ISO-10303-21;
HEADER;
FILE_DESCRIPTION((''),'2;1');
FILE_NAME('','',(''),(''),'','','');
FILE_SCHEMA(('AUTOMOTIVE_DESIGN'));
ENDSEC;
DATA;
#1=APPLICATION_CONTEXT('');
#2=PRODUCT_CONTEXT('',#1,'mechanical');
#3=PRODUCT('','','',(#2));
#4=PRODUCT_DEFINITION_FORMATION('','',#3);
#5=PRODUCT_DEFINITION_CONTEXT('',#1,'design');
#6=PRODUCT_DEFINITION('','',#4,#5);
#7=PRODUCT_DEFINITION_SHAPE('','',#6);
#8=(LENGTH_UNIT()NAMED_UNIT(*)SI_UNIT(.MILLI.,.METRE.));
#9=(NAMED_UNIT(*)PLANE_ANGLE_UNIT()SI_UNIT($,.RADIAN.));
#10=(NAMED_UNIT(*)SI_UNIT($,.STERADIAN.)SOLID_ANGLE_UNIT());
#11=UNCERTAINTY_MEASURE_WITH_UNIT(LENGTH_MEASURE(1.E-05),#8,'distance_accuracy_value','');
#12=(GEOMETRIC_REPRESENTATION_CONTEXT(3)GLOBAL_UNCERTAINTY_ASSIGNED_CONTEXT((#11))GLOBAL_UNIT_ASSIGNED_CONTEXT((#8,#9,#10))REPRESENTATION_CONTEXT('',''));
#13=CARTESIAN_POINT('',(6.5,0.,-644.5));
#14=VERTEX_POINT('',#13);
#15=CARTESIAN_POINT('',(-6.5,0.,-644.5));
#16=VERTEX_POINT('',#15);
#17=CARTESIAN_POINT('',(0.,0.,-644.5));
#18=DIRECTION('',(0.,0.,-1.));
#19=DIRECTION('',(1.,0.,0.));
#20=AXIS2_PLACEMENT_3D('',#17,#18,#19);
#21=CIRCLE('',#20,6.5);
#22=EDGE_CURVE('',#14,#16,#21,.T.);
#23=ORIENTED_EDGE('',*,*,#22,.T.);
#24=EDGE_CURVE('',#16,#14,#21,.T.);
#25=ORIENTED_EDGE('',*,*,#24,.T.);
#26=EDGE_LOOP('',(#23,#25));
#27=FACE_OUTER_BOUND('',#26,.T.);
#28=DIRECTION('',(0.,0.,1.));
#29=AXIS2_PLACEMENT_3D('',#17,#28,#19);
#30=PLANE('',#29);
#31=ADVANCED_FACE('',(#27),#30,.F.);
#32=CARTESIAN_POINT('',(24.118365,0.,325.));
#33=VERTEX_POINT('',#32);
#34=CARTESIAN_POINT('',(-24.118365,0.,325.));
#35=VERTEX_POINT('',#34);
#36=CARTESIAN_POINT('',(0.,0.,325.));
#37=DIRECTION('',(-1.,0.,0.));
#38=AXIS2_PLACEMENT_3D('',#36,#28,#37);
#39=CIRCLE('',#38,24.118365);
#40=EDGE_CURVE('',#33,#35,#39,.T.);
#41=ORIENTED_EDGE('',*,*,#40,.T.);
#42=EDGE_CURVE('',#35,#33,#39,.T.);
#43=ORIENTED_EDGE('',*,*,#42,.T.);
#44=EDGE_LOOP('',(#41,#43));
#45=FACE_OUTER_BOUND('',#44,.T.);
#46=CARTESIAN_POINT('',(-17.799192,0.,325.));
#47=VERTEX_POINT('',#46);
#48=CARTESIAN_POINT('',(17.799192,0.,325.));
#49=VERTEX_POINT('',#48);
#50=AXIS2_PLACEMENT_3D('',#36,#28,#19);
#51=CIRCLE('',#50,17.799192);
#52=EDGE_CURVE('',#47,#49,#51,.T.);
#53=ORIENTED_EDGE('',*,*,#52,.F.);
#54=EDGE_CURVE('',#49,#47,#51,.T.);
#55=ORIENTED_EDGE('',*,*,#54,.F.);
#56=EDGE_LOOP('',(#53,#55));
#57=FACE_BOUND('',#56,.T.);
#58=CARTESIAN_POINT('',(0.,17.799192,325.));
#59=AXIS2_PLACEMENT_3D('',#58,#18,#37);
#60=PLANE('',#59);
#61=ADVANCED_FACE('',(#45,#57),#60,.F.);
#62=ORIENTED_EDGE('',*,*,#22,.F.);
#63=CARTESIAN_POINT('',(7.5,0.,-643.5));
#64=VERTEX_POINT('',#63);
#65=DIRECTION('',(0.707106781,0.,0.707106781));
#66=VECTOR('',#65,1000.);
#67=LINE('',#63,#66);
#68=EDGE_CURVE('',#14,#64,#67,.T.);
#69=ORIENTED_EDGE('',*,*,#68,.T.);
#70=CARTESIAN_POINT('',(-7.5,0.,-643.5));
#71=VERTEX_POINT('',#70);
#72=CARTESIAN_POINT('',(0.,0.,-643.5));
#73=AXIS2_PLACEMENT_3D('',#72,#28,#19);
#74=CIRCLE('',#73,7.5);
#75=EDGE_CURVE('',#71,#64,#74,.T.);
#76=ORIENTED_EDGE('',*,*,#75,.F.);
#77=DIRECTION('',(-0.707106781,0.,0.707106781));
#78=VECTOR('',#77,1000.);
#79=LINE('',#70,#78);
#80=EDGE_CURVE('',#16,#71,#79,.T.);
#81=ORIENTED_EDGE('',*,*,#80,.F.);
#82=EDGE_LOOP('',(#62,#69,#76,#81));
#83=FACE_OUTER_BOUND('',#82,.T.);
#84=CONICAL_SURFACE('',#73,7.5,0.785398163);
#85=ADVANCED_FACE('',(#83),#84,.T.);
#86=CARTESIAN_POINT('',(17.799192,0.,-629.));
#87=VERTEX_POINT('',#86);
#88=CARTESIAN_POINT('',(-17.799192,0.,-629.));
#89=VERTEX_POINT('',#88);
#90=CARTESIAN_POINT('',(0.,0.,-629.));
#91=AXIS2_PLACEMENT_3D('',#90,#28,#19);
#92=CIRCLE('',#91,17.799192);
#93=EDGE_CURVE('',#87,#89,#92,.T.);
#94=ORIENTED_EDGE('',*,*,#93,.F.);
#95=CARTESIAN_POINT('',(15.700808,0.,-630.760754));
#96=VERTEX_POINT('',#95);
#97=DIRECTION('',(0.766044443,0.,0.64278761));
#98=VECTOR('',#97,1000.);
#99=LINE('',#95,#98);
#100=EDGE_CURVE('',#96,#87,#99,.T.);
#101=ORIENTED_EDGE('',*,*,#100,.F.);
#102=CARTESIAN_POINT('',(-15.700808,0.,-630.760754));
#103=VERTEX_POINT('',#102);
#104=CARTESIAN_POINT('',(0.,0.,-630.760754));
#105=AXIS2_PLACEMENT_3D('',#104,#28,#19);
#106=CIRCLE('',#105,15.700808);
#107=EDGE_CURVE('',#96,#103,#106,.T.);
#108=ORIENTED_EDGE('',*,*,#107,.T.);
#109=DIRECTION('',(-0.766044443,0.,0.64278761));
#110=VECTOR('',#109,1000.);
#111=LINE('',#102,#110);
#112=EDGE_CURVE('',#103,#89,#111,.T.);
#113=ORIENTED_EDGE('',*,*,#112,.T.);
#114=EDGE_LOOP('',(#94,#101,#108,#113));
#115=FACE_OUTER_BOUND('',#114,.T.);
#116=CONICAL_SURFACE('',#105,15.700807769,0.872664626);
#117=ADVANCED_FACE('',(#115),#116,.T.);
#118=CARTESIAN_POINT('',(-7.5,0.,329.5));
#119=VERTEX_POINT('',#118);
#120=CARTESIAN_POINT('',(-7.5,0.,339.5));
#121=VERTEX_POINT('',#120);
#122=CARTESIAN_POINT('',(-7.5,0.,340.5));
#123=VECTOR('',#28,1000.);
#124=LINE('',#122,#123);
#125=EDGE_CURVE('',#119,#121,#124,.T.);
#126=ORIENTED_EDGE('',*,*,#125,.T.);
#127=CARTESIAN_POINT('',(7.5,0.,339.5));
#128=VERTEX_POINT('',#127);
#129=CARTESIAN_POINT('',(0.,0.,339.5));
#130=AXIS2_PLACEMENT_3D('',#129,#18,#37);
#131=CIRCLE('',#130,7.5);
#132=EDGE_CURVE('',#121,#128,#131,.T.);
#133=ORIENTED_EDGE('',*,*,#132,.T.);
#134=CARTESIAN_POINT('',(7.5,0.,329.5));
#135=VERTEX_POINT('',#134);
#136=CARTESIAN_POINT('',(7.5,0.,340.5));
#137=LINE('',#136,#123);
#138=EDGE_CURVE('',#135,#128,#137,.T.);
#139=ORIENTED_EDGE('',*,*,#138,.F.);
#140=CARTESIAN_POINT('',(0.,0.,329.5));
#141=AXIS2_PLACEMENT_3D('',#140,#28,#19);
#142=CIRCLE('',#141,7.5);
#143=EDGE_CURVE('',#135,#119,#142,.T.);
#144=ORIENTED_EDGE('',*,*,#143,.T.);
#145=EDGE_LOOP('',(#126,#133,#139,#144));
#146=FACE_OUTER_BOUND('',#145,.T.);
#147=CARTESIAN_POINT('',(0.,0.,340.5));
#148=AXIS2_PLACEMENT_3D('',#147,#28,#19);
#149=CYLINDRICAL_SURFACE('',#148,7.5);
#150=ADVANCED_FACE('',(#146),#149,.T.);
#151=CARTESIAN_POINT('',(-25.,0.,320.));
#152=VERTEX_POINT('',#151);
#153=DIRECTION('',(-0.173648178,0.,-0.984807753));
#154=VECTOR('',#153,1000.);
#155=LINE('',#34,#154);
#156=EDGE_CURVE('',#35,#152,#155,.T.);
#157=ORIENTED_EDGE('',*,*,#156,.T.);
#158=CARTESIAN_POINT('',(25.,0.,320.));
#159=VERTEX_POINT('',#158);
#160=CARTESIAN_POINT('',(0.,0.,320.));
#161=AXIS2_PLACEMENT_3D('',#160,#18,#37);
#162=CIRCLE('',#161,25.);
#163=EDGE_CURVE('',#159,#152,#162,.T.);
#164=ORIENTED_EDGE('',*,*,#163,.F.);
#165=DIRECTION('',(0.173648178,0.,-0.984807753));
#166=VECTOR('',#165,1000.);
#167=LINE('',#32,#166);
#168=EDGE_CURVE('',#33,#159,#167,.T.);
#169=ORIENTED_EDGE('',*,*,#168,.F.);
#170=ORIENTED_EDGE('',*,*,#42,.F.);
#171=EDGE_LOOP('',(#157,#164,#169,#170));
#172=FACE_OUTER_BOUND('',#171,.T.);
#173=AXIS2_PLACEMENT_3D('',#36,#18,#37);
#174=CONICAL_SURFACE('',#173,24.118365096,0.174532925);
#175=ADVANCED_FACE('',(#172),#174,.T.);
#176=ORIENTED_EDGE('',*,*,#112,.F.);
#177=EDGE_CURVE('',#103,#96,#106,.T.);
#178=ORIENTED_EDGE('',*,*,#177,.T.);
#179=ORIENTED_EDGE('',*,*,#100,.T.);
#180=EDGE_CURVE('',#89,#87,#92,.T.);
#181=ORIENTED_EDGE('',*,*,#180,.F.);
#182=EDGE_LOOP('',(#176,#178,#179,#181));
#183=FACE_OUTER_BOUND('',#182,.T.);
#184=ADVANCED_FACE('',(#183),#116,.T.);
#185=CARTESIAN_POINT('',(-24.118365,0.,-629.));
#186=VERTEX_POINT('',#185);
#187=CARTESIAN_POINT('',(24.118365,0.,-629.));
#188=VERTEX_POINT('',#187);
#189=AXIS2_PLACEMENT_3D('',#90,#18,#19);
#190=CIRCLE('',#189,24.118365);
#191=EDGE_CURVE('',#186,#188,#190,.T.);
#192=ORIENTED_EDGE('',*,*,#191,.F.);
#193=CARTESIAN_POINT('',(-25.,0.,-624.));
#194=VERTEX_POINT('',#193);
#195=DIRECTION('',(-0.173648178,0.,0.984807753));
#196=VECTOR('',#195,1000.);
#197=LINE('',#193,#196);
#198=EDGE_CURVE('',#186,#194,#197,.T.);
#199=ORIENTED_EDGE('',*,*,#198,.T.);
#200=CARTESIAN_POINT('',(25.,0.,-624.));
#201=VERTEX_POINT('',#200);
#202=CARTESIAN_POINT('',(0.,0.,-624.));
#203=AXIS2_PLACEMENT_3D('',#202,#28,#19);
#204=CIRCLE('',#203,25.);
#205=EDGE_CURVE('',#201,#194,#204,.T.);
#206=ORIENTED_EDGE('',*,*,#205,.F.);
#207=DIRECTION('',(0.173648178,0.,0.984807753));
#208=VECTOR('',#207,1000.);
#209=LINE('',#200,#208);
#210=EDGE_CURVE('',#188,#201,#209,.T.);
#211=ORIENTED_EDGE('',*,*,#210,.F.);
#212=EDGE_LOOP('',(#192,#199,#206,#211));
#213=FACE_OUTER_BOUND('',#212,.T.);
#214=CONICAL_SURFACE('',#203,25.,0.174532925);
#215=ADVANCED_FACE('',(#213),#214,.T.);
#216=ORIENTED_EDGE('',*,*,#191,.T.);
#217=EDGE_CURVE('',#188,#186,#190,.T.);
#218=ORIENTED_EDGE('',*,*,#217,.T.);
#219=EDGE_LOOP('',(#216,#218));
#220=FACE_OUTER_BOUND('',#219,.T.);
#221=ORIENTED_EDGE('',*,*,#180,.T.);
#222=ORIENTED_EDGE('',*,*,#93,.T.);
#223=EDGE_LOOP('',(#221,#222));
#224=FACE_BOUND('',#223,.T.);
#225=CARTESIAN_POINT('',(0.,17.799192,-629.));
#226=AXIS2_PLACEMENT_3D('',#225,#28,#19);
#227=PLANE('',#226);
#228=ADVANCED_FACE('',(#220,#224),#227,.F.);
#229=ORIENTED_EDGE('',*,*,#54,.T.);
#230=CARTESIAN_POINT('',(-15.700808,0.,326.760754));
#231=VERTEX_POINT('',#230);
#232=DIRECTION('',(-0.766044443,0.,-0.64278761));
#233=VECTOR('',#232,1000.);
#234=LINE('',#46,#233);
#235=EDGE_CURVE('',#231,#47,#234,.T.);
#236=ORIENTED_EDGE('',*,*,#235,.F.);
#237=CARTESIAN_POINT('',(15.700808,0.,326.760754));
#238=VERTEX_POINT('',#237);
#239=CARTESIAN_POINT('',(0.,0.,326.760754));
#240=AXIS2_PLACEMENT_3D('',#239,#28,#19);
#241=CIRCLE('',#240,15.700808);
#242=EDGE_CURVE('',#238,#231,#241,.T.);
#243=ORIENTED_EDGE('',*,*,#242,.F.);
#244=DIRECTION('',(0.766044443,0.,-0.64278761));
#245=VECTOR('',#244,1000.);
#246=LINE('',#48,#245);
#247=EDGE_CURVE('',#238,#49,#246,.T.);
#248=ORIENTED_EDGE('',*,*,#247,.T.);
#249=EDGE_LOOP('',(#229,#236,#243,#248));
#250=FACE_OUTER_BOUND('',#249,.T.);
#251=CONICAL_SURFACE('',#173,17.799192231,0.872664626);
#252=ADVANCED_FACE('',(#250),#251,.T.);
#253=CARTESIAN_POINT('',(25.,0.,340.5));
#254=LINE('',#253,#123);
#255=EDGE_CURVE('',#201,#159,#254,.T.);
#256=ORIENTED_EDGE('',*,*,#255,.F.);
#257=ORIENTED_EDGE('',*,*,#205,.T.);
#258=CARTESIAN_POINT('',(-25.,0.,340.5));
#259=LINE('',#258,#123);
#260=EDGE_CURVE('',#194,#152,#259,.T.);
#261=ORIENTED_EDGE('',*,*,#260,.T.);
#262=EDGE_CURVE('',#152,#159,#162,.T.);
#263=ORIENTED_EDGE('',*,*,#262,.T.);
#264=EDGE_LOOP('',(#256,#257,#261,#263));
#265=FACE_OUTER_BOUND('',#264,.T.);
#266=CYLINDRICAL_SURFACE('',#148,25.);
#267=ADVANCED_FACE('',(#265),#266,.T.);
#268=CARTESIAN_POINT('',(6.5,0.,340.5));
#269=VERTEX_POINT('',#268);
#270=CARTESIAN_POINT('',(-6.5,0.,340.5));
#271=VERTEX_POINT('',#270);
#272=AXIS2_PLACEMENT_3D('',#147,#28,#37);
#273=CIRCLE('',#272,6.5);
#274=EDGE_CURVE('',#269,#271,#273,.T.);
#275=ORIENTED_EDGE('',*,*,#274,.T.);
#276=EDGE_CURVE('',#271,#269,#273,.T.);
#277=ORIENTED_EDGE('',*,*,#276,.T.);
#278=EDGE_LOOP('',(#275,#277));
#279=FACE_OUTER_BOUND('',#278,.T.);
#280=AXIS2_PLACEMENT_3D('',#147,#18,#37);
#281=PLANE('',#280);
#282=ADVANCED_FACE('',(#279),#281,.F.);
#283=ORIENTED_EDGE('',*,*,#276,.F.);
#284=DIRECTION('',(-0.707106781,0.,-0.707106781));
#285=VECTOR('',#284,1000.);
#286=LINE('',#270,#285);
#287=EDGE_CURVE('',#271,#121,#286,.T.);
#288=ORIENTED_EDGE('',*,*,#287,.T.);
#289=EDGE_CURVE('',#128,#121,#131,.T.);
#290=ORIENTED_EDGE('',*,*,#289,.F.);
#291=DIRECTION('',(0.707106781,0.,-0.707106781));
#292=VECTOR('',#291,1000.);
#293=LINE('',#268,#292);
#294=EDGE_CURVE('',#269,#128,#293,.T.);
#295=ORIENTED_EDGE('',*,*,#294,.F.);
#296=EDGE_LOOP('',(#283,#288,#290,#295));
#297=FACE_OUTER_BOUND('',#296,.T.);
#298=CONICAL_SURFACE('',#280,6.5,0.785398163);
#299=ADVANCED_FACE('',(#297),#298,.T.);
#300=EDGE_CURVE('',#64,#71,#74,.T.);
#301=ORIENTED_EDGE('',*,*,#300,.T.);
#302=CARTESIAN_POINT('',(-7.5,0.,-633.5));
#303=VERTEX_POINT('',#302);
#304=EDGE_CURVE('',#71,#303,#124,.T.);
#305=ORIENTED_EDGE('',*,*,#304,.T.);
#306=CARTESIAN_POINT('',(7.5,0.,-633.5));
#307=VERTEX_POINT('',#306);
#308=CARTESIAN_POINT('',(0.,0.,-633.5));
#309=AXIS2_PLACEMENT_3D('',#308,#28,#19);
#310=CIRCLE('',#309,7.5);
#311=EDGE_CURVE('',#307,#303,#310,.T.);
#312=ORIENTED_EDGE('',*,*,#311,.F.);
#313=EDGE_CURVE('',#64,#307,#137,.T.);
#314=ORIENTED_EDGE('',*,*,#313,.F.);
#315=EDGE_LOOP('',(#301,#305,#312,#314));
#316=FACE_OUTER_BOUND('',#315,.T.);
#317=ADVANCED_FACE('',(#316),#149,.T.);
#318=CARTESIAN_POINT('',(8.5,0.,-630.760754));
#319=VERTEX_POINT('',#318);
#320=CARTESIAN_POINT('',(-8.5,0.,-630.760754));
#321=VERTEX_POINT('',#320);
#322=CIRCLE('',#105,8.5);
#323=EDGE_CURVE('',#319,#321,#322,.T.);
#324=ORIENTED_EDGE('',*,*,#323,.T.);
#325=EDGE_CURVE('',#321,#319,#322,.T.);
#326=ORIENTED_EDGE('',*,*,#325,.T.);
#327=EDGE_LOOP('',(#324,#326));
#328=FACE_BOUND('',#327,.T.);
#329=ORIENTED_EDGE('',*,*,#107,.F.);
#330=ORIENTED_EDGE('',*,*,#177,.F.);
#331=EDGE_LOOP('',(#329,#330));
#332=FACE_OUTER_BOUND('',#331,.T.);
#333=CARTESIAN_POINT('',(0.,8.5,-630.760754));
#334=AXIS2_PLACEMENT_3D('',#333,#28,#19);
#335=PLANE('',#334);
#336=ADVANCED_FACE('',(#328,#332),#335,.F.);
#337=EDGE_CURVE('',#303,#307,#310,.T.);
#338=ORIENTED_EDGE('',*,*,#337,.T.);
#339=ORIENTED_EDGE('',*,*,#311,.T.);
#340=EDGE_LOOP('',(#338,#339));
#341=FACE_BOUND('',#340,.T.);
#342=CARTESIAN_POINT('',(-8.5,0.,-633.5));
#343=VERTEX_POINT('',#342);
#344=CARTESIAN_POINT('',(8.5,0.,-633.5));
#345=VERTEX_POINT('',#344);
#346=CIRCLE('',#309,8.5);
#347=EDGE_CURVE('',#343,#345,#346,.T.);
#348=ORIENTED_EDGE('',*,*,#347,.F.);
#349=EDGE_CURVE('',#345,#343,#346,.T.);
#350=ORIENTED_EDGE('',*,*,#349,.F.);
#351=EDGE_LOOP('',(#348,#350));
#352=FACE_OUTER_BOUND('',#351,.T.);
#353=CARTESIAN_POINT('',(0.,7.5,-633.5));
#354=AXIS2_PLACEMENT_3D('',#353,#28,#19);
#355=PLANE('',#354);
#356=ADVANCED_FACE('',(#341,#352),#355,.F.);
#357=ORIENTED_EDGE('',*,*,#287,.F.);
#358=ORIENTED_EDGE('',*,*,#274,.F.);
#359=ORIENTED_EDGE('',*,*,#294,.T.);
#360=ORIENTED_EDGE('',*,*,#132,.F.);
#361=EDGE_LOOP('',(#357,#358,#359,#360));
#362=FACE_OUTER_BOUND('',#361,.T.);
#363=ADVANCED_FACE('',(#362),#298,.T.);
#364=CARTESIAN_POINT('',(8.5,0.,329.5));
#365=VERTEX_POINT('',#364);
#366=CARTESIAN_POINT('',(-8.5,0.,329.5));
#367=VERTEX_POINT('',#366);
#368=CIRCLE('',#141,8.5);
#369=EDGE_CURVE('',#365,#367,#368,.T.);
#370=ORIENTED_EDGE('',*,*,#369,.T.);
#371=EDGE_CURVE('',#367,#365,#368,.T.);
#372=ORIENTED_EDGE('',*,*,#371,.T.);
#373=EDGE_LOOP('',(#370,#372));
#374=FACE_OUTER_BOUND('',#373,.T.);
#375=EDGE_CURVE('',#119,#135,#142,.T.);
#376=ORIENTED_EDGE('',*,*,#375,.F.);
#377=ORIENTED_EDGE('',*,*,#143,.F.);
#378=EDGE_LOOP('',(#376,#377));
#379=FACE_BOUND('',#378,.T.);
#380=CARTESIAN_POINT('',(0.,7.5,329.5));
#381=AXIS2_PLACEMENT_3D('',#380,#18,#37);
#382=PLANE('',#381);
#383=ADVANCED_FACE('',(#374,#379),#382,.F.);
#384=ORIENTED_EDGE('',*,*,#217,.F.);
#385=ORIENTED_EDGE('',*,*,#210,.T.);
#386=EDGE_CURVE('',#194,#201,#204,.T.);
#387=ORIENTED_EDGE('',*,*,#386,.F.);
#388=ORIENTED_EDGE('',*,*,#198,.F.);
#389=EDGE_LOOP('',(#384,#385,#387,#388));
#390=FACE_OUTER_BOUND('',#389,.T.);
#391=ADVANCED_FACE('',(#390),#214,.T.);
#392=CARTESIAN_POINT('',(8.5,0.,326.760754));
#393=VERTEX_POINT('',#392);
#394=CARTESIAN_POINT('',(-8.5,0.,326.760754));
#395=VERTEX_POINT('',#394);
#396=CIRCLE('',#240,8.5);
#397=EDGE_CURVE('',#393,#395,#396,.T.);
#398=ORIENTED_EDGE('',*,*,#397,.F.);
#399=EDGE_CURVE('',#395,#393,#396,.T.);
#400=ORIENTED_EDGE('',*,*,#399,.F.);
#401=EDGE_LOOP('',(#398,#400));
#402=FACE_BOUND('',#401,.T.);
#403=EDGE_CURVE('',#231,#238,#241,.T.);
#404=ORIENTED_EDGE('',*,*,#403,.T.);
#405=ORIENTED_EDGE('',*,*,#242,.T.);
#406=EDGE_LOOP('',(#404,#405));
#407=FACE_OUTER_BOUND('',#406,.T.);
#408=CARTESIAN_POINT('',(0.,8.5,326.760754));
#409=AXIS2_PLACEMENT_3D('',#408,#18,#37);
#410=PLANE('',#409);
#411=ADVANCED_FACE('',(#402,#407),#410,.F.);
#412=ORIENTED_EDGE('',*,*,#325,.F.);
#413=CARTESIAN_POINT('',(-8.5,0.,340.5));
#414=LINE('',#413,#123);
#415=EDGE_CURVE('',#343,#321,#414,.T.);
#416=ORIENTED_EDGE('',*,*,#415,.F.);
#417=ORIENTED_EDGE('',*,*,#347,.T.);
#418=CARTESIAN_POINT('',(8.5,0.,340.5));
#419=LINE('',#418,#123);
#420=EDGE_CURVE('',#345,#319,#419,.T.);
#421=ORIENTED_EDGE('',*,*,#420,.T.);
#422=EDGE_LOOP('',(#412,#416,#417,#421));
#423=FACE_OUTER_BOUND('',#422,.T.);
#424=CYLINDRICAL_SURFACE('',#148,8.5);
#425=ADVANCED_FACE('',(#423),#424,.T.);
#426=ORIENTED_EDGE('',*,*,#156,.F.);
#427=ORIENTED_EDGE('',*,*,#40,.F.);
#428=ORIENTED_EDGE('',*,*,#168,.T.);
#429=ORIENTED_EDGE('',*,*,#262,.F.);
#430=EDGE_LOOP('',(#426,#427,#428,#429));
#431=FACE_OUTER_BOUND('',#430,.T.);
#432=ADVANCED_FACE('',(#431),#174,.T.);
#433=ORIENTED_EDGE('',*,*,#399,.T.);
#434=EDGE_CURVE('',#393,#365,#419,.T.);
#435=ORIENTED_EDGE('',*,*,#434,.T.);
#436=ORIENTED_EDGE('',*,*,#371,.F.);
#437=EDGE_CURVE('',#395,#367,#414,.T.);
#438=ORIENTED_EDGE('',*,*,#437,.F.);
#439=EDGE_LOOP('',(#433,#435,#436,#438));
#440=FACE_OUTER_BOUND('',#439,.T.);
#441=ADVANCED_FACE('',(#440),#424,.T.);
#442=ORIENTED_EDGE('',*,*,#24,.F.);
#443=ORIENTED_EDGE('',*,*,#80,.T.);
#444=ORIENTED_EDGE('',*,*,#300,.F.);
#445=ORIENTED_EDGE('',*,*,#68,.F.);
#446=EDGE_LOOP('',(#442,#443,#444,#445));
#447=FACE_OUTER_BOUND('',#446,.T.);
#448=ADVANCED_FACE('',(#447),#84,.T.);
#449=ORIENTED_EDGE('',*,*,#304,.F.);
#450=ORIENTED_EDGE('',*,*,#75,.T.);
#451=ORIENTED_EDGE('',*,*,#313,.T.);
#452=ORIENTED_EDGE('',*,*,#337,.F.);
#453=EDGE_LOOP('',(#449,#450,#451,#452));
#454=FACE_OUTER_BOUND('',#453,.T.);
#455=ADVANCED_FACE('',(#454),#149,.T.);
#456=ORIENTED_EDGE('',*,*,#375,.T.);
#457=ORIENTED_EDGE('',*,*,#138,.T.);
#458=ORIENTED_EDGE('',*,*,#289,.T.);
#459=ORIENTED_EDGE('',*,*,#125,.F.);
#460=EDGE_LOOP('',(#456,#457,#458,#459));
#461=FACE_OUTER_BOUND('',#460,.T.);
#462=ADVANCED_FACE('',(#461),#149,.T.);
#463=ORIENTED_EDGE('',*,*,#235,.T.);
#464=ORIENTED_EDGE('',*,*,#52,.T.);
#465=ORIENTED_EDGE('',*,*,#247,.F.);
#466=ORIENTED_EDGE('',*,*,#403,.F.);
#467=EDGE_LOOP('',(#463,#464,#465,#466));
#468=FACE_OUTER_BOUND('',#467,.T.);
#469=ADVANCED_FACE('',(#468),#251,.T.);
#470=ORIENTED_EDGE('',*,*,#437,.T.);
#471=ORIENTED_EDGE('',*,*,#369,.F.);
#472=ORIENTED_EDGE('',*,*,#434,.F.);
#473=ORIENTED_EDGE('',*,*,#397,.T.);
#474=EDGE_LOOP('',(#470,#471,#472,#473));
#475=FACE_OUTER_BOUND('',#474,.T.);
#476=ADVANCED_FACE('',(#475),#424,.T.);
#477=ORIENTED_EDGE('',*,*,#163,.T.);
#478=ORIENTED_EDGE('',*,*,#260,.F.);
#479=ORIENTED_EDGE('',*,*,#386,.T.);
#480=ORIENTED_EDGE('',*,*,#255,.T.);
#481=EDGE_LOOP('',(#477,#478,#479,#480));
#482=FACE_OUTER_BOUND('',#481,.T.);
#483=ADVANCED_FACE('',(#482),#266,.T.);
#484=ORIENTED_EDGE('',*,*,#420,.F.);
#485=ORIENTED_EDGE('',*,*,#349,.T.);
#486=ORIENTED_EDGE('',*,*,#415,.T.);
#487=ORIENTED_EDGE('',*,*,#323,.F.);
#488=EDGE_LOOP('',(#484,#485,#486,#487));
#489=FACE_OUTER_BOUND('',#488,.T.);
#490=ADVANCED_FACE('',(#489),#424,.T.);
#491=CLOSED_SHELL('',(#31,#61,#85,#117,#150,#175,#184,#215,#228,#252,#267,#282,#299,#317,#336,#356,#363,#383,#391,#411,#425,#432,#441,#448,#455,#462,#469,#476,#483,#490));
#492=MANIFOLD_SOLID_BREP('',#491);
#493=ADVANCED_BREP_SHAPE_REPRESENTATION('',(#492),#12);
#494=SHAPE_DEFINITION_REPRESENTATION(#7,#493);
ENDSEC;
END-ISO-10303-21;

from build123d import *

# Parameters (mm, degrees)
CHAMFER1_SIZE  = 5
CHAMFER1_SIZE2 = 0.881634904
CHAMFER2_SIZE  = 1


with BuildPart() as part:
    # Sketch3 → Revolve1 (revolve)
    with BuildSketch(Plane(origin=(0, 0, 0), x_dir=(0, 0, -1), z_dir=(1, 0, 0)), mode=Mode.PRIVATE) as revolve1_sk:
        Polygon((-325, 25), (629, 25), (629, 17.799192231), (630.760753628, 15.700807769), (630.760753628, 8.5), (633.5, 8.5), (633.5, 7.5), (644.5, 7.5), (644.5, 0), (-340.5, 0), (-340.5, 7.5), (-329.5, 7.5), (-329.5, 8.5), (-326.760753628, 8.5), (-326.760753628, 15.700807769), (-325, 17.799192231), align=None)
    revolve(revolve1_sk.sketch.rotate(Axis((0, 0, 340.5), (0, 0, -1)), 90), axis=Axis((0, 0, 340.5), (0, 0, -1)))

    # Chamfer1
    chamfer1_edges = [part.edges().sort_by_distance(p)[0] for p in [
        (-25, 0, -629),
        (-25, 0, 325),
    ]]
    chamfer1_side = [part.faces().sort_by_distance(p)[0] for p in [
        (-25, 0, -152),
    ]]
    chamfer(chamfer1_edges, length=CHAMFER1_SIZE, length2=CHAMFER1_SIZE2, reference=chamfer1_side[0])

    # Chamfer2
    chamfer2_edges = [part.edges().sort_by_distance(p)[0] for p in [
        (-7.5, 0, 340.5),
        (-7.5, 0, -644.5),
    ]]
    chamfer(chamfer2_edges, length=CHAMFER2_SIZE)


solid = part.part
